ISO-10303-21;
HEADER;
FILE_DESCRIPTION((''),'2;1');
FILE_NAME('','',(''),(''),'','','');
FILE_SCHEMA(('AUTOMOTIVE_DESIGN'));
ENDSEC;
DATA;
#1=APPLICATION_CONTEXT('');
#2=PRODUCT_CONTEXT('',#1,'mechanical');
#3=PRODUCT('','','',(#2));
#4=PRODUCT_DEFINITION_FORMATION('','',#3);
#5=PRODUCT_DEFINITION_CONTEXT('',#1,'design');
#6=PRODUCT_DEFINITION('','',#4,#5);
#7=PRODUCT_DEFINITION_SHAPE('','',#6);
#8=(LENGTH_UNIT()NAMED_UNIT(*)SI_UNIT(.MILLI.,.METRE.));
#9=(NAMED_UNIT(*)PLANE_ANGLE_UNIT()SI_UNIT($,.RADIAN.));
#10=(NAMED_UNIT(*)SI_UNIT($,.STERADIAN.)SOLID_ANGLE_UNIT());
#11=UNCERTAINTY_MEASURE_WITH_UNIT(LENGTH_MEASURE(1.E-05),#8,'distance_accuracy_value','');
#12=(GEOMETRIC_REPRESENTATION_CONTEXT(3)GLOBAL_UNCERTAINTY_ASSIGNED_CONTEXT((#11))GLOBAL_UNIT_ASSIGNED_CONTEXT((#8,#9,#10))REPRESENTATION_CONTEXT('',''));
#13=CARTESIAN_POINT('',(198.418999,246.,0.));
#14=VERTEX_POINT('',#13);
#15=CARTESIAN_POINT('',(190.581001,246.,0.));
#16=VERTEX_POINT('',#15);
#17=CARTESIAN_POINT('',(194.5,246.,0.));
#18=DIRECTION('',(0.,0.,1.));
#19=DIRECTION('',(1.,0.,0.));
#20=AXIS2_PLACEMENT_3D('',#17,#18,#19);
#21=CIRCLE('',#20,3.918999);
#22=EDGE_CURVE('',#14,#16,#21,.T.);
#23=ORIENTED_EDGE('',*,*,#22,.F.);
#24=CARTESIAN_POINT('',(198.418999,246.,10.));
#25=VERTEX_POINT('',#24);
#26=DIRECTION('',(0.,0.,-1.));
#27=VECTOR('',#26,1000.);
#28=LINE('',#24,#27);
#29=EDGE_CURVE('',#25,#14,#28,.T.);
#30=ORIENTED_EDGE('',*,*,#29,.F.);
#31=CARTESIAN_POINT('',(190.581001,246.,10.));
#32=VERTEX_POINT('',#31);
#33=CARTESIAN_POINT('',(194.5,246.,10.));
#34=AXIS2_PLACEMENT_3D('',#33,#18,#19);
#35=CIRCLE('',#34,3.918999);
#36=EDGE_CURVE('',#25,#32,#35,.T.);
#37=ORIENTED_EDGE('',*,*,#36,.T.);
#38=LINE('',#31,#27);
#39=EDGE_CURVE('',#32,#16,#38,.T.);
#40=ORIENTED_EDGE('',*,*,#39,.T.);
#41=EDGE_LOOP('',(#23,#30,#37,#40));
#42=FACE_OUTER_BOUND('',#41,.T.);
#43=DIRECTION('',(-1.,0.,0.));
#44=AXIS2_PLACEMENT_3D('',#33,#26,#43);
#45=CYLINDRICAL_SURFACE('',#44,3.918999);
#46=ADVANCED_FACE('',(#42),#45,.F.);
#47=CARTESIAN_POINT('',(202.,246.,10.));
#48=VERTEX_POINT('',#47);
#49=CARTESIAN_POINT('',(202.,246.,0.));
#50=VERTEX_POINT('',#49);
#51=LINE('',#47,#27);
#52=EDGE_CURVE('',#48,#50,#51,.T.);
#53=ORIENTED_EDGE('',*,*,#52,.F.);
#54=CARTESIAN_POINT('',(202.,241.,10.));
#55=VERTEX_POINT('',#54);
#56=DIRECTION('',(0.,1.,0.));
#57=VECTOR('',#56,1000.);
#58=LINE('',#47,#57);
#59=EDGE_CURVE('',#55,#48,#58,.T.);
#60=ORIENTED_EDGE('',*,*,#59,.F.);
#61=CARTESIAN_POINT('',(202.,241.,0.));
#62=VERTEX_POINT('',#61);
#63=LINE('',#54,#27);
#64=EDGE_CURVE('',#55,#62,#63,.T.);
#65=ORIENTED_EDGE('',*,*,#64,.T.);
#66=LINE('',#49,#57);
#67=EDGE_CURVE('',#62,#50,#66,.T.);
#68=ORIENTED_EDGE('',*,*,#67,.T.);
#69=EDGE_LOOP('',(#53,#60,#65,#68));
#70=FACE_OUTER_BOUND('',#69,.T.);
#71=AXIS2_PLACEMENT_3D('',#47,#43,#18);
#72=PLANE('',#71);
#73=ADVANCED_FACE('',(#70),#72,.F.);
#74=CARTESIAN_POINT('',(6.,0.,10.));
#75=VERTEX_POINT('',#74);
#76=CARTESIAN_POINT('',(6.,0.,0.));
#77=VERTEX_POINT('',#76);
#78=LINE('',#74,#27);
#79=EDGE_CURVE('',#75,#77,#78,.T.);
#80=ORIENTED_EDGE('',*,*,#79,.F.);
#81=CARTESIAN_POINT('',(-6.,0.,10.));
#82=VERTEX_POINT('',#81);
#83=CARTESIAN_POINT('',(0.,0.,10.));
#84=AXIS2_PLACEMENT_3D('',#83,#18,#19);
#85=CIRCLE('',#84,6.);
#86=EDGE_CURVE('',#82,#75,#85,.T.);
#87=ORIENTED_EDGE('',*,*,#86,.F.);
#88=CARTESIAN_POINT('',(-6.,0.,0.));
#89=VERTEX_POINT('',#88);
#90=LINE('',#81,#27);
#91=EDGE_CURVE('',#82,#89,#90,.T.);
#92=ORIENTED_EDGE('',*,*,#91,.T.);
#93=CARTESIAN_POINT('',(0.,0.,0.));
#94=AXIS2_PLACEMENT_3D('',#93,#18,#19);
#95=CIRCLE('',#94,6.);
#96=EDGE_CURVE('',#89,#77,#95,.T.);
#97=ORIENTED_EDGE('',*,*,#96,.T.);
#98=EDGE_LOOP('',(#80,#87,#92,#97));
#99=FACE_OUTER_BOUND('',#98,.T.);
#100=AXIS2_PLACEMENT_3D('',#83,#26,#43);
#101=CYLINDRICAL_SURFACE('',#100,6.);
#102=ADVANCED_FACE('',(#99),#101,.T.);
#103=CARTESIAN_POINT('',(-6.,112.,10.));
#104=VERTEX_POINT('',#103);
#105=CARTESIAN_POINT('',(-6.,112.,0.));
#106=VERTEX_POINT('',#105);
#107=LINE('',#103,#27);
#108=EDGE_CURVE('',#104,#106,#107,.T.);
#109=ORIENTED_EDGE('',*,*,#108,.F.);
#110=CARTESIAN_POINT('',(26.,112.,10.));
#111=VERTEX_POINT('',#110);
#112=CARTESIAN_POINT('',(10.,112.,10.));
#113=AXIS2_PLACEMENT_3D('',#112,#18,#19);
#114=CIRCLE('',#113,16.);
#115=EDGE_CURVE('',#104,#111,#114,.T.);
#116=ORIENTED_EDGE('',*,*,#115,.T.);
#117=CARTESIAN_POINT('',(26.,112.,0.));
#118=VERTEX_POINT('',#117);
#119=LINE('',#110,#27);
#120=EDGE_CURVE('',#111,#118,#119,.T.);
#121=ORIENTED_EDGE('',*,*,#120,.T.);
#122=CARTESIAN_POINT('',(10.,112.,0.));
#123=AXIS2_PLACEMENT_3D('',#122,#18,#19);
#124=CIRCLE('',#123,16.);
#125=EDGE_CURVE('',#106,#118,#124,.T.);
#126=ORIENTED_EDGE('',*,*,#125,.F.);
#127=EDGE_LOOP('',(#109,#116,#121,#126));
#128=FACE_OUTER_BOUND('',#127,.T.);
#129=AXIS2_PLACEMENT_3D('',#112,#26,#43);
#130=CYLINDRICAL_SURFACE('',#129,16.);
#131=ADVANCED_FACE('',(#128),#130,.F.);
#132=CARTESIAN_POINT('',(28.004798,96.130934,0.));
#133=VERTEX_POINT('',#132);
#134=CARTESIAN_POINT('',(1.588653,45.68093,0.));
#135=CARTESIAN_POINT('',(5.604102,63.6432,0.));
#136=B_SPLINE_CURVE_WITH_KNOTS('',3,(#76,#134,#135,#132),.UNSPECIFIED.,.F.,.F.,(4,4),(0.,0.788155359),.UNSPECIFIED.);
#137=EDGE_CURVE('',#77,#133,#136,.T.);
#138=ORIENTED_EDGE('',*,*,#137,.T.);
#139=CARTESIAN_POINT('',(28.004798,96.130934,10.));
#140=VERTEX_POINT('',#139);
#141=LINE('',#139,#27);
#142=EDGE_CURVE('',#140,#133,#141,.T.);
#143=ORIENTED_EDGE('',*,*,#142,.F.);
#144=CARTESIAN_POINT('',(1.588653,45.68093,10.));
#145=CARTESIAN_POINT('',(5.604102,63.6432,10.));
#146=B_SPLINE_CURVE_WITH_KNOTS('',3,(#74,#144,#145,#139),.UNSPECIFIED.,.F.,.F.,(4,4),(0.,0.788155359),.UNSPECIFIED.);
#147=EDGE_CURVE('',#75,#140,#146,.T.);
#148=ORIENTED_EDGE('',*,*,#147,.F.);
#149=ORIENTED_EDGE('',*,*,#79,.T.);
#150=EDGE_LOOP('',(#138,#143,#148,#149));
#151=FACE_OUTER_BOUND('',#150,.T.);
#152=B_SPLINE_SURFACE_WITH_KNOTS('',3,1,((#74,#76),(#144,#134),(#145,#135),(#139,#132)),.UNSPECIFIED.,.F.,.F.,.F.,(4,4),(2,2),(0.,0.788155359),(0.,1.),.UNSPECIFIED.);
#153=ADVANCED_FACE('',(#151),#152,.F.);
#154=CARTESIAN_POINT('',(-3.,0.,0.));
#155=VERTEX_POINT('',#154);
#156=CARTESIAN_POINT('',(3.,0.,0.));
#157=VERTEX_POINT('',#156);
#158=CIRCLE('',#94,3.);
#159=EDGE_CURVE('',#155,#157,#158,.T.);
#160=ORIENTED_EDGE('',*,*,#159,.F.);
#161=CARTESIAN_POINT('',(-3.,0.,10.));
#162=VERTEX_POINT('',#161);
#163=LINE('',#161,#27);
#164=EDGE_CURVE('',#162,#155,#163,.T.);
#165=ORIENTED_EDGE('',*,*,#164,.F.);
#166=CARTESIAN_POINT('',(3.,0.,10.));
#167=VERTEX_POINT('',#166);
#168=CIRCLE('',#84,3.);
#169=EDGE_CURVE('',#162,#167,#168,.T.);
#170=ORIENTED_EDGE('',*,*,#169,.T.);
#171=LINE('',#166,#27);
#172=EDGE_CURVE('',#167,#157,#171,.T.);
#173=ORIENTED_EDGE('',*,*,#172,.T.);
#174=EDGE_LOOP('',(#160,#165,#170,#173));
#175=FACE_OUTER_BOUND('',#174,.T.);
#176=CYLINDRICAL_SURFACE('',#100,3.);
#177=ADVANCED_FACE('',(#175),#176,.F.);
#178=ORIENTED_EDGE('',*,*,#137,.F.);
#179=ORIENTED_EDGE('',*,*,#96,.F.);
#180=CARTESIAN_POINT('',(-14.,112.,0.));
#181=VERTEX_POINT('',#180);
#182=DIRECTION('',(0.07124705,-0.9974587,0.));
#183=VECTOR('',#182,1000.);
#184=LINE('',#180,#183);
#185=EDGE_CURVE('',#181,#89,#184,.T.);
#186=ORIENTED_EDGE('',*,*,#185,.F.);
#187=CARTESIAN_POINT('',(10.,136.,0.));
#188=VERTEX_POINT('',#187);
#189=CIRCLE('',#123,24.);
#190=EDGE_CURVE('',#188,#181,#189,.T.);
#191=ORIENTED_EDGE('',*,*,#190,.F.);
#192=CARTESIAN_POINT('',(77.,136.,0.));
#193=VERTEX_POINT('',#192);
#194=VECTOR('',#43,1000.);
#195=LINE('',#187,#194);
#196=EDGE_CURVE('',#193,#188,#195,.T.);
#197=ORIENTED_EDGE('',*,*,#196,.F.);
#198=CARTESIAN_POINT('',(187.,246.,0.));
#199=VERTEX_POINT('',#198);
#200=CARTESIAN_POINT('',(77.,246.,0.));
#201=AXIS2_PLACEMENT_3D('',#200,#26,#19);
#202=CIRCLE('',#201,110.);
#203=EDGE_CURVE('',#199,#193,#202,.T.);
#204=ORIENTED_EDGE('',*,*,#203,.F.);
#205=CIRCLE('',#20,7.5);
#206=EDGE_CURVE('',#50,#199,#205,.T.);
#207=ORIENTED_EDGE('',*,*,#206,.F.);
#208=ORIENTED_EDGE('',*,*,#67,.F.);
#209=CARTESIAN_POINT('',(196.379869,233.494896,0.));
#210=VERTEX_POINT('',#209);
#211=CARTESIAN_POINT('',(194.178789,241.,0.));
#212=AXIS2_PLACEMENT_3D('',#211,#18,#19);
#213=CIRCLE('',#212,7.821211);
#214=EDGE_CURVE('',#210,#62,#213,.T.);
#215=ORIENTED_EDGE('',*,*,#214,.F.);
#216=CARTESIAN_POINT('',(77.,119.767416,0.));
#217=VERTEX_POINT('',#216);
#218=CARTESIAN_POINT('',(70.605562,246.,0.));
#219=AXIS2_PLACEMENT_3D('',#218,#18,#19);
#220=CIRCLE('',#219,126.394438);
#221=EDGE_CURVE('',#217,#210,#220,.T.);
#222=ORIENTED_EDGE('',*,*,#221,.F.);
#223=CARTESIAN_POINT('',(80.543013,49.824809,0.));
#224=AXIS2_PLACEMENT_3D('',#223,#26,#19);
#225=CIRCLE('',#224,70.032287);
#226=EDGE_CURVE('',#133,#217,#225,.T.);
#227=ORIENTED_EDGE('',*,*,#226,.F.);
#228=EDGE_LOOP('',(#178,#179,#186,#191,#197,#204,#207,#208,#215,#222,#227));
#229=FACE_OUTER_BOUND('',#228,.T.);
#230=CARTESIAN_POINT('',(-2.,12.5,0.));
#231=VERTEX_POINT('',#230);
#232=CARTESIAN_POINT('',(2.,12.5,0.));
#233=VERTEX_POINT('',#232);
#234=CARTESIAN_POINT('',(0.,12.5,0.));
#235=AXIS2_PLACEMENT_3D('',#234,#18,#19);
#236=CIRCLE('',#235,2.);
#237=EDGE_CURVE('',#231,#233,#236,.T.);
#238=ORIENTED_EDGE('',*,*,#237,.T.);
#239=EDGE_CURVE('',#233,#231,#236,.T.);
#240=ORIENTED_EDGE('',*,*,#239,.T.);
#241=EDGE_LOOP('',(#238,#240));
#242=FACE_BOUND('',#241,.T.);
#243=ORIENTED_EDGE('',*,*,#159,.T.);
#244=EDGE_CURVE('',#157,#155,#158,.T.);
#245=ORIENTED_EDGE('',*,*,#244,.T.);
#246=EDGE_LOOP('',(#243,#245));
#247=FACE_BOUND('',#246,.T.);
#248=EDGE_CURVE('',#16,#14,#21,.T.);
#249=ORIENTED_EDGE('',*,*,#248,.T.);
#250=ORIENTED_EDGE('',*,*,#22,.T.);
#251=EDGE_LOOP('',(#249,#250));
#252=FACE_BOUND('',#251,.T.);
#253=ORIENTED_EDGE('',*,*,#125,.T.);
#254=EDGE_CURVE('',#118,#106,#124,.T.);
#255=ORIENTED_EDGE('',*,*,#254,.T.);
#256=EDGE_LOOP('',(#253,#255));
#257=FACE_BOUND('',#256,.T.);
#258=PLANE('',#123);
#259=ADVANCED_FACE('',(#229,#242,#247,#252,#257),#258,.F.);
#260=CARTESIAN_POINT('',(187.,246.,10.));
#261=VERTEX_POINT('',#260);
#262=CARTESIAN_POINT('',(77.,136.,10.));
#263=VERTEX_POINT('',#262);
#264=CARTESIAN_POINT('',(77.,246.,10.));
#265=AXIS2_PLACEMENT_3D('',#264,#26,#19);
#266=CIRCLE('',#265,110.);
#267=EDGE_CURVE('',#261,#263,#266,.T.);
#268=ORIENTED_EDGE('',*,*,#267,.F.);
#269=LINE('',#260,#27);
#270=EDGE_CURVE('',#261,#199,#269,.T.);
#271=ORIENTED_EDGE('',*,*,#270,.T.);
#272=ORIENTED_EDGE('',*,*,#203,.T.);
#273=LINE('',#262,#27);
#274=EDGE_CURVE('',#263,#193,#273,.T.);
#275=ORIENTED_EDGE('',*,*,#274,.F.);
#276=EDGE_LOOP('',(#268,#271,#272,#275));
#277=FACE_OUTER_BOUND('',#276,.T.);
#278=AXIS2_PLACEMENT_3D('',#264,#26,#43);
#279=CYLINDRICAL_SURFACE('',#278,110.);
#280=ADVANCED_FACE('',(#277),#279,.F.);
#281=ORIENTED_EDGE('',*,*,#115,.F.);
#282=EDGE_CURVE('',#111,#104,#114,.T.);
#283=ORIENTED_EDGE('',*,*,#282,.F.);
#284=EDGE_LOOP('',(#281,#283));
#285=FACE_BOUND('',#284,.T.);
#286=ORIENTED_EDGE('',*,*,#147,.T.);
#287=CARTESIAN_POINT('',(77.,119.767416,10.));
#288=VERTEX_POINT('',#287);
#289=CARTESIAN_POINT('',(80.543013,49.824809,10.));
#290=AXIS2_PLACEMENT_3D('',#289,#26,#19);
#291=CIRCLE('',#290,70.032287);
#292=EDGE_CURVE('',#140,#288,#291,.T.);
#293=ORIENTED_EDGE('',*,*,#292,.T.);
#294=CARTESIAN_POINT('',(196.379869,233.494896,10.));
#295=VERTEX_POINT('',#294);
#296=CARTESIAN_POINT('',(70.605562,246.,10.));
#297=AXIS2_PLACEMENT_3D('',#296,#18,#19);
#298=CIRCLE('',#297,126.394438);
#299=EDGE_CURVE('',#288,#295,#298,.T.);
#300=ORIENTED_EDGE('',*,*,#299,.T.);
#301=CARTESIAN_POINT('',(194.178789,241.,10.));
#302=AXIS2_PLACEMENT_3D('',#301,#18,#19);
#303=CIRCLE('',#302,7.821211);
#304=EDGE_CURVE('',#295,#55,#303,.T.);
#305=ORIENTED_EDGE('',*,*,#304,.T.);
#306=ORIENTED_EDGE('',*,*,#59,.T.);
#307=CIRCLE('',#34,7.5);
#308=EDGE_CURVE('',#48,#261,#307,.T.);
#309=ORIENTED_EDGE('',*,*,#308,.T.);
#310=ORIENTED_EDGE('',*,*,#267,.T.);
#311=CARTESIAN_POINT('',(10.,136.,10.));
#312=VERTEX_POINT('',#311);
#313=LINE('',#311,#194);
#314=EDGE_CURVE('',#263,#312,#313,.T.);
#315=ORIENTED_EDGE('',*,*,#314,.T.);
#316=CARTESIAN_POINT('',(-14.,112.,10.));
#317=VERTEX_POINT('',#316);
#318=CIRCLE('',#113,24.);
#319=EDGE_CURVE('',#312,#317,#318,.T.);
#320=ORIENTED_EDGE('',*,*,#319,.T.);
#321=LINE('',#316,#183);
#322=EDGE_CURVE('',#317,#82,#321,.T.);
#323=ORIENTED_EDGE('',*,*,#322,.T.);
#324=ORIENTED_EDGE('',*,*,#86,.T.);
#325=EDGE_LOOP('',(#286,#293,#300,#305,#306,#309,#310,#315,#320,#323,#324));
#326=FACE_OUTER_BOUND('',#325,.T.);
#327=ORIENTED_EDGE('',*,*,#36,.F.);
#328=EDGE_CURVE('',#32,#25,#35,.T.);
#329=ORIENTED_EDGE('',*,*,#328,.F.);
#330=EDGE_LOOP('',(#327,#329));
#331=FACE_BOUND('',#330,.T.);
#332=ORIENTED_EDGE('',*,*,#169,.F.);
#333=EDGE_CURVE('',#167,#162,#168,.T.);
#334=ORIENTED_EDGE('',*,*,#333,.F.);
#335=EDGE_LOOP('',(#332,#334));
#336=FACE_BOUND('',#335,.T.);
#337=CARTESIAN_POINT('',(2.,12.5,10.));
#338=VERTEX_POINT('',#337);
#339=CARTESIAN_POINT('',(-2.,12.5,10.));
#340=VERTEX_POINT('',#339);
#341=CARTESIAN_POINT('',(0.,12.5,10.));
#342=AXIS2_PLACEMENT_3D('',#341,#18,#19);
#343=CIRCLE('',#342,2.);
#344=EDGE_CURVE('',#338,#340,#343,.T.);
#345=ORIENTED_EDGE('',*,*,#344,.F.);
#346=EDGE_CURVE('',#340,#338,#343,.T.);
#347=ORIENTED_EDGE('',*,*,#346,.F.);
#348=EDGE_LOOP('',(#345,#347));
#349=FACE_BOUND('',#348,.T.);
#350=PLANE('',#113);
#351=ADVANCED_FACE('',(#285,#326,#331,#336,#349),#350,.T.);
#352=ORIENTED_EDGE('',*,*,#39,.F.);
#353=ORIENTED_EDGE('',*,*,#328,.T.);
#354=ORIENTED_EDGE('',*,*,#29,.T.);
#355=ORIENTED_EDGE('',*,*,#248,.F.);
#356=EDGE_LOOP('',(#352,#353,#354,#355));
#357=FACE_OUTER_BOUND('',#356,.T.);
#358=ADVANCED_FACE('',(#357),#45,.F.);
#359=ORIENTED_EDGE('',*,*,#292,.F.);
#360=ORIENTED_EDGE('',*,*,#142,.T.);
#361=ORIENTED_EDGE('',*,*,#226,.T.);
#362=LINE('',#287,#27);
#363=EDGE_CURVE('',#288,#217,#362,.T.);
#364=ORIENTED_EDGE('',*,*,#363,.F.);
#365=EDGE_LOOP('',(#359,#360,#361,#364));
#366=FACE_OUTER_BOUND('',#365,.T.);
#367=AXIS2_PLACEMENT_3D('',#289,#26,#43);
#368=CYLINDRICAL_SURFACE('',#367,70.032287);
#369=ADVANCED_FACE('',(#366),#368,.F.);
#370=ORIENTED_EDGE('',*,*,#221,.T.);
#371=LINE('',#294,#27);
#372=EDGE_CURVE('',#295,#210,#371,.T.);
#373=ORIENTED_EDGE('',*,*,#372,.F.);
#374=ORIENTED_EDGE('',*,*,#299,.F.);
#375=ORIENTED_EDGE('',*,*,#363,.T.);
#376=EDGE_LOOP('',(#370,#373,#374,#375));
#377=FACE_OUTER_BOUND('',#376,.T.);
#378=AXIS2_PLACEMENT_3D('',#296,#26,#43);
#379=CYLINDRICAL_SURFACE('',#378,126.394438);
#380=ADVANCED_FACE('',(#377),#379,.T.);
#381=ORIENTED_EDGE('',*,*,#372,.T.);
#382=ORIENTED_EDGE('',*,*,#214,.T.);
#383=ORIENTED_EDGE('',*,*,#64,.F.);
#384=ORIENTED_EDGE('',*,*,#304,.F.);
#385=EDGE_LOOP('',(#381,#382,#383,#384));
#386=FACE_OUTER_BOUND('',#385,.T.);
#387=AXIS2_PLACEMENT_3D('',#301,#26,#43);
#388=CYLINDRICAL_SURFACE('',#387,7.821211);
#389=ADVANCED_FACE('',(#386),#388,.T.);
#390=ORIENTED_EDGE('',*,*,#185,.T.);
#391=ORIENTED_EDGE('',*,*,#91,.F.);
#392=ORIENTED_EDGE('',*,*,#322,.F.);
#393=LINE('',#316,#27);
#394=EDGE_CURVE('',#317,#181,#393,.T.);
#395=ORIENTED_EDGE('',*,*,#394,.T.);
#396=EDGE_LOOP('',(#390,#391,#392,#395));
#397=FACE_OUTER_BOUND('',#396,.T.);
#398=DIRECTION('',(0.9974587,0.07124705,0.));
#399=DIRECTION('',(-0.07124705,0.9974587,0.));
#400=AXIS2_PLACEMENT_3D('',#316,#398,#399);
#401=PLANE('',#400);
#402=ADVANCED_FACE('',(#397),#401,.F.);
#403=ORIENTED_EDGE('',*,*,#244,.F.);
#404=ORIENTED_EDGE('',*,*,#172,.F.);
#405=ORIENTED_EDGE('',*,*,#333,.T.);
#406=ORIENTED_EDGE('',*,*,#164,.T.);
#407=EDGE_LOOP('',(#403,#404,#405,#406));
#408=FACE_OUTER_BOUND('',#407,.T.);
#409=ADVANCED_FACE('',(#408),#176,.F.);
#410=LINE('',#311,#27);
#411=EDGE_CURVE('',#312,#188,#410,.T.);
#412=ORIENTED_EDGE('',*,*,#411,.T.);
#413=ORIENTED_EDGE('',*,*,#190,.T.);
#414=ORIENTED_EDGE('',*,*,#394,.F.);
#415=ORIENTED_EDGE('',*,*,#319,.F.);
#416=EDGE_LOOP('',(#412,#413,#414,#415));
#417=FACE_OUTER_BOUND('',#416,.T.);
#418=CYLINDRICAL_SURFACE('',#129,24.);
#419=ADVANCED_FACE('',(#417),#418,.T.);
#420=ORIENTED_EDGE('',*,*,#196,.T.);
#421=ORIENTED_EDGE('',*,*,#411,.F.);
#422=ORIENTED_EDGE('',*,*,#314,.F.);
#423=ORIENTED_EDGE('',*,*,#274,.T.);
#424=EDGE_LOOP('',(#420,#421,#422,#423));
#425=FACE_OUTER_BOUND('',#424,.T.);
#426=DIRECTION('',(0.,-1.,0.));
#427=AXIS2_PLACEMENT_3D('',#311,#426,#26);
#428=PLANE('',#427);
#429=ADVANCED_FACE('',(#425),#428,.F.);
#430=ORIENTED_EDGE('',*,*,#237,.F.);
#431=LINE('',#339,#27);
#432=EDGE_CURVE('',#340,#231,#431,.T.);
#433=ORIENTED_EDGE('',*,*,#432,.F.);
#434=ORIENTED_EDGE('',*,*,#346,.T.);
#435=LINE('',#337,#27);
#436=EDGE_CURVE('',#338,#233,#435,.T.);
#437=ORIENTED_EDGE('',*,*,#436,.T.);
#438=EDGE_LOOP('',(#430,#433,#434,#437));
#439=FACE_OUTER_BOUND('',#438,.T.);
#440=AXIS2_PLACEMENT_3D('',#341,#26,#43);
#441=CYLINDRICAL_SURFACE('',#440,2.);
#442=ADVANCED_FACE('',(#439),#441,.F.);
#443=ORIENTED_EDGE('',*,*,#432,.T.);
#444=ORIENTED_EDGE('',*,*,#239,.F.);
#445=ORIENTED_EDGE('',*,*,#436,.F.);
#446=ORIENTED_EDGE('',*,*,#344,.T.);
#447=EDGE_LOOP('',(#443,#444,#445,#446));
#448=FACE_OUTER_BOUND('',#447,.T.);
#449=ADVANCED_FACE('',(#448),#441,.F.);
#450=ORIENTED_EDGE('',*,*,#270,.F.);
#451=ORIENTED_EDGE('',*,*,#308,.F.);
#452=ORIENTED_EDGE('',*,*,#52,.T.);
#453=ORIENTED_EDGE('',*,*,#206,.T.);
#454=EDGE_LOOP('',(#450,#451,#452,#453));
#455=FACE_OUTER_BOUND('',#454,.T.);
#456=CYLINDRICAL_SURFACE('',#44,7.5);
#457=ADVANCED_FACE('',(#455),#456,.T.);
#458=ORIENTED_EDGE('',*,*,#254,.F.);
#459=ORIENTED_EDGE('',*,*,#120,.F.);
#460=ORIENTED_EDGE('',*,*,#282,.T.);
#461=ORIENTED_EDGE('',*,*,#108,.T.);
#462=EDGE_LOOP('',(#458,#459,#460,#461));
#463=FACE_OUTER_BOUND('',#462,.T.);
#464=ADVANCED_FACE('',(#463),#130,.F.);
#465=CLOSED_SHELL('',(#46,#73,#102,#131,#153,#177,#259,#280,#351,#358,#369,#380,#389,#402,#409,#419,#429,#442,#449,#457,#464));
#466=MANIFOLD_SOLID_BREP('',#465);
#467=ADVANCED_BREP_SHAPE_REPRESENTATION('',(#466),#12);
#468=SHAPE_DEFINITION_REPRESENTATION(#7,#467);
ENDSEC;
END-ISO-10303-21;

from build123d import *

# Parameters (mm, degrees)
SKETCH_1_R      = 3
SKETCH_1_R_2    = 16
SKETCH_1_R_3    = 3.91899873
SKETCH_1_R_4    = 2
EXTRUDE_1_DEPTH = 10


with BuildPart() as part:
    # 草图1 → 凸台-拉伸1 (new body)
    with BuildSketch(Plane.XY):
        with BuildLine():
            Line((-14, 112), (-6, 0))
            ThreePointArc((-6, 0), (0, -6), (6, 0))
            add(Edge.make_bspline(
                [(6, 0), (1.588652615, 45.680929706), (5.604102499, 63.643200211), (28.004797731, 96.13093391)],
                knots=[0, 0, 0, 0, 0.788155359, 0.788155359, 0.788155359, 0.788155359], degree=3))
            ThreePointArc((28.004797731, 96.13093391), (50.113637924, 112.900750568), (77, 119.767416406))
            ThreePointArc((77, 119.767416406), (157.787149523, 154.485384951), (196.379869136, 233.494896157))
            ThreePointArc((196.379869136, 233.494896157), (200.439238403, 236.311917913), (202, 241))
            Line((202, 241), (202, 246))
            ThreePointArc((202, 246), (194.5, 253.5), (187, 246))
            ThreePointArc((187, 246), (154.781745931, 168.218254069), (77, 136))
            Line((77, 136), (10, 136))
            ThreePointArc((10, 136), (-6.970562748, 128.970562748), (-14, 112))
        make_face()
        Circle(SKETCH_1_R, mode=Mode.SUBTRACT)
        with Locations((10, 112)):
            Circle(SKETCH_1_R_2, mode=Mode.SUBTRACT)
        with Locations((194.5, 246)):
            Circle(SKETCH_1_R_3, mode=Mode.SUBTRACT)
        with Locations((0, 12.5)):
            Circle(SKETCH_1_R_4, mode=Mode.SUBTRACT)
    extrude(amount=EXTRUDE_1_DEPTH)


solid = part.part
